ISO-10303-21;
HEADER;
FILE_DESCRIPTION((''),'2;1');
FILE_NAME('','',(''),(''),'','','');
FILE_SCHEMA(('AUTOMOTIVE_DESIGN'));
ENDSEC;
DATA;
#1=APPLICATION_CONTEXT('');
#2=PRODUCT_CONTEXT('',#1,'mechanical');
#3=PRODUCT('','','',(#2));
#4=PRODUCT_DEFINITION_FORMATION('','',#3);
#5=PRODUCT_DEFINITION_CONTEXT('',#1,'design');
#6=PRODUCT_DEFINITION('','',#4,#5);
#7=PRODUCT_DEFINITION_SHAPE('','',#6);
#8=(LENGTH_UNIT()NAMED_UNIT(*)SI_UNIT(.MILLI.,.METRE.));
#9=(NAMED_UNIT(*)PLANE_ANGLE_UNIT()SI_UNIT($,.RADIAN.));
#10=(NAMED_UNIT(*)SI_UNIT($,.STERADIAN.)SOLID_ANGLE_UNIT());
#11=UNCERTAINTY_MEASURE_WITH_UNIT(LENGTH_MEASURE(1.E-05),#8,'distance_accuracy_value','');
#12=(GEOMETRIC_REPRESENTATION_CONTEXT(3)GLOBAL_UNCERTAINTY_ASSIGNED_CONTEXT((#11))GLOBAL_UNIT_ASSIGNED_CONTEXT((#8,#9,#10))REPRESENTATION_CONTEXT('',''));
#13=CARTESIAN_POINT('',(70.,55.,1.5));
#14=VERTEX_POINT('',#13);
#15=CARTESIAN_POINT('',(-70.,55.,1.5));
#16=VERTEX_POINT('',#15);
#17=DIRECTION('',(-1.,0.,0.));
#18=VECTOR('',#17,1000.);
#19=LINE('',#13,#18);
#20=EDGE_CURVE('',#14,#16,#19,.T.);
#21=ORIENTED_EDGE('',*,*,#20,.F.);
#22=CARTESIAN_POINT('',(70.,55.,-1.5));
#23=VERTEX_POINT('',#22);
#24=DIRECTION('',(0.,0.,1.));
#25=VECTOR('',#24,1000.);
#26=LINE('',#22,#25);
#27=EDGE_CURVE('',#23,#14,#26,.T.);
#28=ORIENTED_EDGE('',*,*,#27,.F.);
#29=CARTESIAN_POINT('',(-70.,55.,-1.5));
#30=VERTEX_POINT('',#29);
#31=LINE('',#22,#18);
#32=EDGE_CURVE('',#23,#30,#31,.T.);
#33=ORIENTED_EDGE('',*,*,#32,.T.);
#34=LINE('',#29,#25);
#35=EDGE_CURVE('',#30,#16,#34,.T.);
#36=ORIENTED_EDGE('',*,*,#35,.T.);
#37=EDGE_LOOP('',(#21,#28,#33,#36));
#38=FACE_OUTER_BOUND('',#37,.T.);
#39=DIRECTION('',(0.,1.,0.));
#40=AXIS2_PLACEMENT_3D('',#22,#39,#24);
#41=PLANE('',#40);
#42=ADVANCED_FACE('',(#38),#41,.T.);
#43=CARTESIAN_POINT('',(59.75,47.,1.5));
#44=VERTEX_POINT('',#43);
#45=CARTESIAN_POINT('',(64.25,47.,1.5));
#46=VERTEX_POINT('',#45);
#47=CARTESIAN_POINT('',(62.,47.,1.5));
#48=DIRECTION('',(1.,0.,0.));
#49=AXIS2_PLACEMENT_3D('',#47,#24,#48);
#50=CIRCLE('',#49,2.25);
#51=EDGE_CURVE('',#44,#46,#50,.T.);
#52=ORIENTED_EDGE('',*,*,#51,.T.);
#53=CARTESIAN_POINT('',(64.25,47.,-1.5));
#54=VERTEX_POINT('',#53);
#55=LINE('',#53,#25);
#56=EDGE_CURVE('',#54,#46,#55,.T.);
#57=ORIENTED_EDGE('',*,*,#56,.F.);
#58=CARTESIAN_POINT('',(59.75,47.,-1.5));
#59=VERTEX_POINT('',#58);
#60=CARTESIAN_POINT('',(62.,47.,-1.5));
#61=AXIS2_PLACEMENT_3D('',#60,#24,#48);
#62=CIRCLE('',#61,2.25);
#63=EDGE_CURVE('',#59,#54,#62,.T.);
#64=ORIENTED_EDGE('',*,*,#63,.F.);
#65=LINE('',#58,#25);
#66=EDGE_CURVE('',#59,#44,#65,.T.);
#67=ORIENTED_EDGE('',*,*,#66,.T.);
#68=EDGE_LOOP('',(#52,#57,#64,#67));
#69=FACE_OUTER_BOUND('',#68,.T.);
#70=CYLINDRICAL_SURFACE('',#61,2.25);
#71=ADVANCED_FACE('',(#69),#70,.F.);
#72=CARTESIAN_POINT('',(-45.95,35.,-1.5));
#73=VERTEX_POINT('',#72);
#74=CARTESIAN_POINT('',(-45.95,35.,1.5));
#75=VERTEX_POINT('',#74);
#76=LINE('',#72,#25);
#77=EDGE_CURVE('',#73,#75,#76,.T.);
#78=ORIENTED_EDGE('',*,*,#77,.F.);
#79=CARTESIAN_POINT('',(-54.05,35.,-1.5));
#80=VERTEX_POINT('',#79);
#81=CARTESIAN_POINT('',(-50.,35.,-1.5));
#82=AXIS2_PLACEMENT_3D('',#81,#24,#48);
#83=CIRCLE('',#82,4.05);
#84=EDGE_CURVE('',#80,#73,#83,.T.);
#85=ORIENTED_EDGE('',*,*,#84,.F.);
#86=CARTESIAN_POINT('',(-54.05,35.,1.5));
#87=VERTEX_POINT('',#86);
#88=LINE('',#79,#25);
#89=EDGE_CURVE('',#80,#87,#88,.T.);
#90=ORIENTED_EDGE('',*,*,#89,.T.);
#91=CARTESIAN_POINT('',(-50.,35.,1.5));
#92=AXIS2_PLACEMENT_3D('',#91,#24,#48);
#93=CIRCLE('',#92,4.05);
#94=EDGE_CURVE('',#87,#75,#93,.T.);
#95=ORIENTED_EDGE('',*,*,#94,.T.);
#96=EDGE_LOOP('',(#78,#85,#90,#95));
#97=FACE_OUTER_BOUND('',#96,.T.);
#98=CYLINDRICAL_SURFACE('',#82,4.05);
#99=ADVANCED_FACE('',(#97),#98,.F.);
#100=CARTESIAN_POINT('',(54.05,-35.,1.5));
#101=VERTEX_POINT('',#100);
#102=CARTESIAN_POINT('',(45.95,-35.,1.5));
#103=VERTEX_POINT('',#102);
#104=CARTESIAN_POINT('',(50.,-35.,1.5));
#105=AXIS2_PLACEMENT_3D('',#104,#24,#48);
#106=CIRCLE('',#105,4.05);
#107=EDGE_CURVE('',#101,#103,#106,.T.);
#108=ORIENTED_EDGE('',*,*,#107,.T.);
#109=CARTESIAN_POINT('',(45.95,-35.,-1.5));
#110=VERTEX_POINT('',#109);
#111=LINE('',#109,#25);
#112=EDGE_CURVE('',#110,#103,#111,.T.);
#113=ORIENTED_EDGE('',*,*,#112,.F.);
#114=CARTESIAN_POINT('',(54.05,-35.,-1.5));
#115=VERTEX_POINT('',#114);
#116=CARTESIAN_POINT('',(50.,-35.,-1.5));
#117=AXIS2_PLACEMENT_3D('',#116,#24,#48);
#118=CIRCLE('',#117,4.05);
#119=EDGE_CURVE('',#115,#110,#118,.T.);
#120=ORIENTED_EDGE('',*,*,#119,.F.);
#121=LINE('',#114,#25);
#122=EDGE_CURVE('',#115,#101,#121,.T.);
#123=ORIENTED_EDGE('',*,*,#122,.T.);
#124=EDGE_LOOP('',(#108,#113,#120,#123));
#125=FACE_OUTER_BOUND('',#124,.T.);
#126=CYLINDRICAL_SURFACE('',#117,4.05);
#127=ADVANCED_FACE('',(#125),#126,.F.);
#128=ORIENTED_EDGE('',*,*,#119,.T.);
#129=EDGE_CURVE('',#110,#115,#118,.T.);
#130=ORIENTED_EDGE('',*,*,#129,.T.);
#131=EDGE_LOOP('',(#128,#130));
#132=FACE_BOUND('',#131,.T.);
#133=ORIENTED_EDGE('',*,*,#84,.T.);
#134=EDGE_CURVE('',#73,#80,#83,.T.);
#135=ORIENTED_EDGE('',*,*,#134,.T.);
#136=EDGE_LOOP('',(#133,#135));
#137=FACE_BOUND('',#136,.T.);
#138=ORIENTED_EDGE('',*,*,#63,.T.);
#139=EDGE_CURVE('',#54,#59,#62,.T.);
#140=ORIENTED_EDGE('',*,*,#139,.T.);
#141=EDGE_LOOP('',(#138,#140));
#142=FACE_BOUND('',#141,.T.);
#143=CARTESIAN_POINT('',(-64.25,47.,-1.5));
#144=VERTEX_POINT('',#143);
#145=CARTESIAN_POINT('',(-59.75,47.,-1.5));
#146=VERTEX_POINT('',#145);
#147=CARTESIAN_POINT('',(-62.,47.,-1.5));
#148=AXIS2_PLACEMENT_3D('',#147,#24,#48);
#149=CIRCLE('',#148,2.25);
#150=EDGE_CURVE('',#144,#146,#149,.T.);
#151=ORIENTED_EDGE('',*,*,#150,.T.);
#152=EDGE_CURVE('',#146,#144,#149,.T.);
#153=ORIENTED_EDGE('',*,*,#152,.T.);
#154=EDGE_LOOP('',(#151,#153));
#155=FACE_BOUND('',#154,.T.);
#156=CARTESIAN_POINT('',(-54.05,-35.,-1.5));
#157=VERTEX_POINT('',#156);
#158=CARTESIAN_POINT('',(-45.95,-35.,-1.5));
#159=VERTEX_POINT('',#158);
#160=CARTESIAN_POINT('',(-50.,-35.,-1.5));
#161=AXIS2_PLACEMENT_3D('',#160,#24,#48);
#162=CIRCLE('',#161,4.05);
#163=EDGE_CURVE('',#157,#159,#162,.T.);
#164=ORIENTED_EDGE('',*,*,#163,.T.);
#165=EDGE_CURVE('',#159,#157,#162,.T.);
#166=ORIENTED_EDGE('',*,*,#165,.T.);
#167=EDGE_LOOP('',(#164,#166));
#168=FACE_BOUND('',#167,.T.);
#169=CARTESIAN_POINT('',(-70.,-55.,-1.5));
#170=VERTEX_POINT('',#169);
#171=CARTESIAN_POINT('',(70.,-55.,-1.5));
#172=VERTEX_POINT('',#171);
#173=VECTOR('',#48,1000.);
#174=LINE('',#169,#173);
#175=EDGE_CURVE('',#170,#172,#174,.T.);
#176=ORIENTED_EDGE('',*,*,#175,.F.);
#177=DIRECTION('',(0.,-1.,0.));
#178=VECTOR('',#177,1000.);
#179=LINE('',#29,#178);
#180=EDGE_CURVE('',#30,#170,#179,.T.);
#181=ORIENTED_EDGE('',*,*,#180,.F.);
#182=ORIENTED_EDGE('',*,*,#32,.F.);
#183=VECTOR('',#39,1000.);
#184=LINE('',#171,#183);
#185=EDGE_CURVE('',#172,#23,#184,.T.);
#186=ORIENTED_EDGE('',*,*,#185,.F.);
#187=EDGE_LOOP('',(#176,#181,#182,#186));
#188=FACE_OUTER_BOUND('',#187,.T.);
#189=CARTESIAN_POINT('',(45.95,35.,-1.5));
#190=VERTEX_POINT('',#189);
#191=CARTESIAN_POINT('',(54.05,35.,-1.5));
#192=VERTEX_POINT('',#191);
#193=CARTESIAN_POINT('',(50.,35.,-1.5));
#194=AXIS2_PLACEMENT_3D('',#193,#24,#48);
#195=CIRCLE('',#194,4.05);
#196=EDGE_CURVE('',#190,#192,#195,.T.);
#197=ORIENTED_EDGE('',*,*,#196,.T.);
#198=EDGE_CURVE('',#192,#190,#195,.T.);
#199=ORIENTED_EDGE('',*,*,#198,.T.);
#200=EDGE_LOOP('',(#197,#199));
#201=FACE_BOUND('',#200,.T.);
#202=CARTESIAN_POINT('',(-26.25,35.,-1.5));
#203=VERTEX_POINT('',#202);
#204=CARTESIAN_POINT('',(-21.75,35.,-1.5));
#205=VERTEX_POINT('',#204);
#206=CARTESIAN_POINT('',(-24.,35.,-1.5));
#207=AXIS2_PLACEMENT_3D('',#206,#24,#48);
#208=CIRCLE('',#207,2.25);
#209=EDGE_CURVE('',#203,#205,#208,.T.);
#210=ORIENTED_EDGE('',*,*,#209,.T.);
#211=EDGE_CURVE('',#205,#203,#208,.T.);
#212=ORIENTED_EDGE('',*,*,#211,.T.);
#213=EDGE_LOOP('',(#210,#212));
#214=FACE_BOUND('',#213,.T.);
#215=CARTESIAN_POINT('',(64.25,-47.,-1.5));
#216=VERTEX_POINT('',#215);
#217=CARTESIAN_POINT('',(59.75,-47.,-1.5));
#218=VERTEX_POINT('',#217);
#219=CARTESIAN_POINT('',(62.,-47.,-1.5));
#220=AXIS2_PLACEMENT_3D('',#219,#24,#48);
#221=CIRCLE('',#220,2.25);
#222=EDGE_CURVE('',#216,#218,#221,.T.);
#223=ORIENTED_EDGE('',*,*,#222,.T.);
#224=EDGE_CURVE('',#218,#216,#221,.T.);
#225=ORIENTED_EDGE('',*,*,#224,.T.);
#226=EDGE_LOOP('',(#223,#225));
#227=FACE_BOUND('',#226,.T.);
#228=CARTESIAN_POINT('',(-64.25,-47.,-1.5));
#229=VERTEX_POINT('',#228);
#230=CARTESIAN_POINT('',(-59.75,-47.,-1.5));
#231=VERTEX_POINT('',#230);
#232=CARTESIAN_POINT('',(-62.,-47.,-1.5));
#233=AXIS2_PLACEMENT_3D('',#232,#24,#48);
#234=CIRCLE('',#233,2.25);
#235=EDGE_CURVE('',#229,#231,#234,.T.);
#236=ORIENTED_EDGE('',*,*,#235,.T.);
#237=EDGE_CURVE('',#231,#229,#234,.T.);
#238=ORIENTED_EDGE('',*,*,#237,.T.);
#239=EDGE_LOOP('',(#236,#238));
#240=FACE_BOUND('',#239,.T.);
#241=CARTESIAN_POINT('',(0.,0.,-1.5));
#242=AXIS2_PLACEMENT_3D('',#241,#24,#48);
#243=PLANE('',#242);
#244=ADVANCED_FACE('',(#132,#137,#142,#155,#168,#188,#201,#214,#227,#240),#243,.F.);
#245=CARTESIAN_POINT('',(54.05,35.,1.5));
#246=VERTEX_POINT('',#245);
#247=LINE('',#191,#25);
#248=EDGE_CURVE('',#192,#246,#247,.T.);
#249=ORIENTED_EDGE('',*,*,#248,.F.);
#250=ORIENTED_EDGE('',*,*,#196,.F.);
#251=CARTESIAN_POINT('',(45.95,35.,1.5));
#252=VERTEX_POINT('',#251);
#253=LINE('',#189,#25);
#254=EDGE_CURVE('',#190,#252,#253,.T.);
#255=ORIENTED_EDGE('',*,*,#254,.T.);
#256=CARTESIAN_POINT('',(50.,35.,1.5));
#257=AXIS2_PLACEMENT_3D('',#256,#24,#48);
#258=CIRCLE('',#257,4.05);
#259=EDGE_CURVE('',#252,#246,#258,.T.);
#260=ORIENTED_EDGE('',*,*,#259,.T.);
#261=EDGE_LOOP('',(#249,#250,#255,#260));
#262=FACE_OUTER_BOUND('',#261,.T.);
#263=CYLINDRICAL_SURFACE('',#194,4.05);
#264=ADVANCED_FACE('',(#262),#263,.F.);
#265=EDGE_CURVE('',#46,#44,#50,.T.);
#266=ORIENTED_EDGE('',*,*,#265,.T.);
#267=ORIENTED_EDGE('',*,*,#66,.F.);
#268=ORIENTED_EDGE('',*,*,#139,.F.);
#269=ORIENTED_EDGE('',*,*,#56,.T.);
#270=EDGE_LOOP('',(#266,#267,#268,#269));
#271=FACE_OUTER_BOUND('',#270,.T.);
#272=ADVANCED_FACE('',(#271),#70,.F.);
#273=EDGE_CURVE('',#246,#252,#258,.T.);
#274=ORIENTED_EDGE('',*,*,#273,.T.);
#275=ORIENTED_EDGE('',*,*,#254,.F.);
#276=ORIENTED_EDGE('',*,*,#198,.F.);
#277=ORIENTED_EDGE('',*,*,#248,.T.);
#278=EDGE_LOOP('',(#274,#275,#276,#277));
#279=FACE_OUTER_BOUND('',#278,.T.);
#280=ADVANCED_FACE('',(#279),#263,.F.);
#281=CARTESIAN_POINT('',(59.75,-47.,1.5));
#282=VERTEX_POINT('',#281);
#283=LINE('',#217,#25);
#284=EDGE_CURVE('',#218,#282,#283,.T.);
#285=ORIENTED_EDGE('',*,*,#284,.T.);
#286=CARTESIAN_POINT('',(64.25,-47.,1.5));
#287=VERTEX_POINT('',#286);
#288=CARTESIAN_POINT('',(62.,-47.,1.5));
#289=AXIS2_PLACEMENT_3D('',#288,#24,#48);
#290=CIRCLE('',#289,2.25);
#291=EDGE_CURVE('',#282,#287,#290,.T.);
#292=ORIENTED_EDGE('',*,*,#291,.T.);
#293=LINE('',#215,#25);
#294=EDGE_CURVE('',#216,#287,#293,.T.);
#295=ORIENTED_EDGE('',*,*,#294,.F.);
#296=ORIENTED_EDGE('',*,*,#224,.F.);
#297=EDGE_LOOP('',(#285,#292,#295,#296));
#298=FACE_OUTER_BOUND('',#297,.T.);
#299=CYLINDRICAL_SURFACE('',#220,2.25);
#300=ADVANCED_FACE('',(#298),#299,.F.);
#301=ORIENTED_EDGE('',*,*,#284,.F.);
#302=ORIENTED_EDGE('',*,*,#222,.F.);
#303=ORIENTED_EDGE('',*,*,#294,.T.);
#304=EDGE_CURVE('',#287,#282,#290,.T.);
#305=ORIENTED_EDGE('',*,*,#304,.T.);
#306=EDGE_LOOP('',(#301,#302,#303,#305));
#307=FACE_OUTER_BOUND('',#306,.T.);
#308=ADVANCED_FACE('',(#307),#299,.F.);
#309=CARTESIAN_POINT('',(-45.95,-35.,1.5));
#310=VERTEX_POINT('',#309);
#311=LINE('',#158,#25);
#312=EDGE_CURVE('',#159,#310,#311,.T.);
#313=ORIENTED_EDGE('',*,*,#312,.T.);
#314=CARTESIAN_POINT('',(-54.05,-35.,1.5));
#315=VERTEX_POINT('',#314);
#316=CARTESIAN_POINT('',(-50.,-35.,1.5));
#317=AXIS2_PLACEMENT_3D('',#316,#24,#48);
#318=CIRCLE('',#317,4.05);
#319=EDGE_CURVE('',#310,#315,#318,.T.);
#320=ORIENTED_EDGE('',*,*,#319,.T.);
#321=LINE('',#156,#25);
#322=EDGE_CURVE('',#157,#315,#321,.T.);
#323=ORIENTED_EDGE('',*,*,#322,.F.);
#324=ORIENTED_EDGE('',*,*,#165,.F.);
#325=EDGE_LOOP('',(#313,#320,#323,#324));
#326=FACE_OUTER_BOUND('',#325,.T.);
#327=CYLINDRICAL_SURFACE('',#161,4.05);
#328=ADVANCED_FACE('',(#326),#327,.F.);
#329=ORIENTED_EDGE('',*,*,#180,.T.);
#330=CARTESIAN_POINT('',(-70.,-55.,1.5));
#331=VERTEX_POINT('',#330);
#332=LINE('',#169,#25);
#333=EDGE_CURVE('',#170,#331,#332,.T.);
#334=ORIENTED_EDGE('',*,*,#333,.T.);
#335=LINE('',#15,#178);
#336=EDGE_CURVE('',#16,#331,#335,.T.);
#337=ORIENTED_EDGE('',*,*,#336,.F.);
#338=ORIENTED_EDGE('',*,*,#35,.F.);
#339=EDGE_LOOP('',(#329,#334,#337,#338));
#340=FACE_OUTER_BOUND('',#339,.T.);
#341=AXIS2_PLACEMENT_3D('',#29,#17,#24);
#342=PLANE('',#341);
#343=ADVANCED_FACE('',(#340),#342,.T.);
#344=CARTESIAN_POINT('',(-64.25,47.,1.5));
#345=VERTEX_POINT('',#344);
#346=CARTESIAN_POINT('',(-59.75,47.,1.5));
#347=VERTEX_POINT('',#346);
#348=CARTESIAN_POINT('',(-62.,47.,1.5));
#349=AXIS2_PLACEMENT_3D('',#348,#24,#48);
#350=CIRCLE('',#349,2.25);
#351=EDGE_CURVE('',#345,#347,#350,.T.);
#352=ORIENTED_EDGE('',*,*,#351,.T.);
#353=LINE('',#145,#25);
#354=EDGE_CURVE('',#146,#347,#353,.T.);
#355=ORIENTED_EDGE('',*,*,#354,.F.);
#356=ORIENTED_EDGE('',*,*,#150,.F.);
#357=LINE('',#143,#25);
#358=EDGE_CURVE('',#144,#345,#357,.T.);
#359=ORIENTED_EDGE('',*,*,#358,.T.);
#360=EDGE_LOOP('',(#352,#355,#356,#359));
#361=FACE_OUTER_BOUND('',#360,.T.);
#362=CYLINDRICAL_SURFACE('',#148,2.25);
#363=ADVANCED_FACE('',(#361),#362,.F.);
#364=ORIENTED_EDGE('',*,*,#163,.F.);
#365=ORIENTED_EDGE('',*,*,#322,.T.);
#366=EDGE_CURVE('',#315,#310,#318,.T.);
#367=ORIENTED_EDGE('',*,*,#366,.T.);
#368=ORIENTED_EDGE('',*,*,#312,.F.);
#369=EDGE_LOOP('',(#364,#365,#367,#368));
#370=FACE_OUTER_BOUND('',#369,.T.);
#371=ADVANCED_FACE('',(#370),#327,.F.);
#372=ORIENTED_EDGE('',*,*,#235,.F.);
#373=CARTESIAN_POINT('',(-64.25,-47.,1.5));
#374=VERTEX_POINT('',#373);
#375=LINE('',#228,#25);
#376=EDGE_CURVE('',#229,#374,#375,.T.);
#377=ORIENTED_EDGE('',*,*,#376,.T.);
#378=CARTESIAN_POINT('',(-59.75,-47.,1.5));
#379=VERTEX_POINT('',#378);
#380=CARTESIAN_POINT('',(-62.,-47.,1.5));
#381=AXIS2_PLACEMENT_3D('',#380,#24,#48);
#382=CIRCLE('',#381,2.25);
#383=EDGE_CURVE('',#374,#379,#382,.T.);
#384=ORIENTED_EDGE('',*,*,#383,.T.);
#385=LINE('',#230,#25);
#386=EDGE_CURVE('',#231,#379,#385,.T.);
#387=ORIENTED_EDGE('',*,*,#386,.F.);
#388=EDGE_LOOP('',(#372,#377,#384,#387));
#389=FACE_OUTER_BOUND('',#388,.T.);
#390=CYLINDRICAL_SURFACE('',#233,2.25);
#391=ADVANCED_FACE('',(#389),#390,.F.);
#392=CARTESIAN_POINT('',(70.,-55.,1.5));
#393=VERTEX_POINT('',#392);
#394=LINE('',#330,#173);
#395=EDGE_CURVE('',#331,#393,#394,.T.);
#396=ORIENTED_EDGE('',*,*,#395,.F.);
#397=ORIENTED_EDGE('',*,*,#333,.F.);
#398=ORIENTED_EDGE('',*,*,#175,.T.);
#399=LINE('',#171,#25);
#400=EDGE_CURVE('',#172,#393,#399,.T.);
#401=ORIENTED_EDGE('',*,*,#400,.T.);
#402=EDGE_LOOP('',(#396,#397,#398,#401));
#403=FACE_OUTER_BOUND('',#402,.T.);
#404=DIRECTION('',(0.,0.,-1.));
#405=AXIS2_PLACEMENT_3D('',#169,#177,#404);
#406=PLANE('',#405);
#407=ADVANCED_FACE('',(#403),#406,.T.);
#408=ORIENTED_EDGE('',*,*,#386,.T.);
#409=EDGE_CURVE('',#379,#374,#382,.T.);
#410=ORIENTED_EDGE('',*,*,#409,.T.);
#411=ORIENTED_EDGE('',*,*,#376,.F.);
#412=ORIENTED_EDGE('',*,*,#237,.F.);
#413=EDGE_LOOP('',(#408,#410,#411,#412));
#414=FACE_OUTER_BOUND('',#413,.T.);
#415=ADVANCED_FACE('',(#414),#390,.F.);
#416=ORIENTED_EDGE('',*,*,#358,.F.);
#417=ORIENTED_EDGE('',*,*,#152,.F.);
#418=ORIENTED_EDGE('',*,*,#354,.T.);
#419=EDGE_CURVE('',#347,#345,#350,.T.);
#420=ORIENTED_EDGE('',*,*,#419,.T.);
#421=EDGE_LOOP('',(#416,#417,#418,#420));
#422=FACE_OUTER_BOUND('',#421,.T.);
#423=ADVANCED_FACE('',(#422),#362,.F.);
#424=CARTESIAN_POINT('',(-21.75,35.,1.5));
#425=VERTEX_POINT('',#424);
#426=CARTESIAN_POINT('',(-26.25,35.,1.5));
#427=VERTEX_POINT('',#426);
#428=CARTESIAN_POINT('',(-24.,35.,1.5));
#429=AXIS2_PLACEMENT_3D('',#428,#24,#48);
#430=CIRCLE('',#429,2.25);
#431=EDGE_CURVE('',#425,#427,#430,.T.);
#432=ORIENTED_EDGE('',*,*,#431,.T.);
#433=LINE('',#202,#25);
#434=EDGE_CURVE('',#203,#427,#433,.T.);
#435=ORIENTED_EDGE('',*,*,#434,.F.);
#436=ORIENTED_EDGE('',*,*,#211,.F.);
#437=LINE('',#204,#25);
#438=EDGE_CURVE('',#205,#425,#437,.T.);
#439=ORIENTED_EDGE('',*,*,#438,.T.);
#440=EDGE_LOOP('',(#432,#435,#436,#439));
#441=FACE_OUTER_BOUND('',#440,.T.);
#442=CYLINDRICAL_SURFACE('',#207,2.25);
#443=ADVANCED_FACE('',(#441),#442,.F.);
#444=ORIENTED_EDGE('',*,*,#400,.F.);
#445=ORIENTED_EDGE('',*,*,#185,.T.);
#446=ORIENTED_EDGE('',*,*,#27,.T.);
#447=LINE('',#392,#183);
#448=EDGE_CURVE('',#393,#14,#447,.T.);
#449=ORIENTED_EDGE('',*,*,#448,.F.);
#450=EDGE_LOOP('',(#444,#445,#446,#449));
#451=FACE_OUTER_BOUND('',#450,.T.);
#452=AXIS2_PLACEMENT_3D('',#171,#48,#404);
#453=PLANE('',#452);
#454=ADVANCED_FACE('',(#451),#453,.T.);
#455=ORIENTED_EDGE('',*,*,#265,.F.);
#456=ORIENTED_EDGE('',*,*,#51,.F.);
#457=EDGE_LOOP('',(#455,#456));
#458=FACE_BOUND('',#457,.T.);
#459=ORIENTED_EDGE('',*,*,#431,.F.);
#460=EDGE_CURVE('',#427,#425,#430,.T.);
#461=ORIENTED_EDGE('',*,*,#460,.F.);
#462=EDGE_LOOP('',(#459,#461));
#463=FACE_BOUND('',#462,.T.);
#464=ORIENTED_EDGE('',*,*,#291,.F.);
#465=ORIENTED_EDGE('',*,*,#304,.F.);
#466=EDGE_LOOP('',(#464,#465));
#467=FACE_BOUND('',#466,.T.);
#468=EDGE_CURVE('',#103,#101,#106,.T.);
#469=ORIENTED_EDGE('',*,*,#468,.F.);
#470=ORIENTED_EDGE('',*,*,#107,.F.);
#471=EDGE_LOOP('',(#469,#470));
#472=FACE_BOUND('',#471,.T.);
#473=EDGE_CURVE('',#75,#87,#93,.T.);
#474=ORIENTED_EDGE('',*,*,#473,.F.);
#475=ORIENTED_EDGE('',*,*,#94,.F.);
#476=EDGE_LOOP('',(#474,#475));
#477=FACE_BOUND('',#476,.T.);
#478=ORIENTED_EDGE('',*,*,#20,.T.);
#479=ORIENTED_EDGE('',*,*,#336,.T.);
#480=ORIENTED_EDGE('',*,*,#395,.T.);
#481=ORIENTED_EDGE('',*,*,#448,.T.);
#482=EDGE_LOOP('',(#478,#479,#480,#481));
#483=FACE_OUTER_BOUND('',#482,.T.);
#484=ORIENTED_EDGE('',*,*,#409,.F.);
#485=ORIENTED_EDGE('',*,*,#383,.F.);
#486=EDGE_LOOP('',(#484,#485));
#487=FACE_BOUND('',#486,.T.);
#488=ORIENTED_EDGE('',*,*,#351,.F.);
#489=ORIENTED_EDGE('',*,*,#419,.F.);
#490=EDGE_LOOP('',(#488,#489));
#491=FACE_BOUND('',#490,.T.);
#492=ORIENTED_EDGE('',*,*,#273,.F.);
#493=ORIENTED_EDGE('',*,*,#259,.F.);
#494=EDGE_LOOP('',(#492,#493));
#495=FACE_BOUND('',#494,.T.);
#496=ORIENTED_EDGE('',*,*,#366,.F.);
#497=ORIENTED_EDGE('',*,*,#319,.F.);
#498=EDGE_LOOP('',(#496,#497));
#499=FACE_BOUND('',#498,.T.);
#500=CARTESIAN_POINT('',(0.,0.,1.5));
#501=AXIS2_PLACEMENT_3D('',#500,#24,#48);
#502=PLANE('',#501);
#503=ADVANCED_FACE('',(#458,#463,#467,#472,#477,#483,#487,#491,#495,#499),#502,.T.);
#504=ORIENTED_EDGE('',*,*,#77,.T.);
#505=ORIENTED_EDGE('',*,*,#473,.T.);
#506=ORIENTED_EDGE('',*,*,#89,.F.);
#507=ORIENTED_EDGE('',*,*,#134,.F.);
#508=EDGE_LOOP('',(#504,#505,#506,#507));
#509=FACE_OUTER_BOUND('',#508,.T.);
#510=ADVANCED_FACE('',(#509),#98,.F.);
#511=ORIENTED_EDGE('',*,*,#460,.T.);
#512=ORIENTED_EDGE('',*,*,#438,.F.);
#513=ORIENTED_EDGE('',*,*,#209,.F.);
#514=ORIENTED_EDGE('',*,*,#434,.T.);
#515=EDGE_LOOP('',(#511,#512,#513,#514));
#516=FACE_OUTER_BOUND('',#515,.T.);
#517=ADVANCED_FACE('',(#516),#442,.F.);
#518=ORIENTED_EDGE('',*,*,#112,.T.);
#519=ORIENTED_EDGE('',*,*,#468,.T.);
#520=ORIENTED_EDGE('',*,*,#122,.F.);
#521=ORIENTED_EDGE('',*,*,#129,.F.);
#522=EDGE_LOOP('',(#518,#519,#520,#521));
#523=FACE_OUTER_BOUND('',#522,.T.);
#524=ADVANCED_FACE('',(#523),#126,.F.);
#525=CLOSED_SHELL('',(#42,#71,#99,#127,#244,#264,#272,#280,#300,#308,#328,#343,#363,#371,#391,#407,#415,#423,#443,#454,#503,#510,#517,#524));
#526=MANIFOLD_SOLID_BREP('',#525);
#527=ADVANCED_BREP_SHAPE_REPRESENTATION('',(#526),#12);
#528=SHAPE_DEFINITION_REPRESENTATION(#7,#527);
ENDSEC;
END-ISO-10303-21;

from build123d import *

# Parameters (mm, degrees)
SKETCH_1_W      = 140
SKETCH_1_H      = 110
SKETCH_1_R      = 2.25
SKETCH_1_R_2    = 4.05
EXTRUDE_1_DEPTH = 1.5


with BuildPart() as part:
    # 草图1 → 凸台-拉伸1 (new, symmetric)
    with BuildSketch(Plane.XY):
        Rectangle(SKETCH_1_W, SKETCH_1_H)
        with Locations((-62, -47)):
            Circle(SKETCH_1_R, mode=Mode.SUBTRACT)
        with Locations((-62, 47)):
            Circle(SKETCH_1_R, mode=Mode.SUBTRACT)
        with Locations((62, -47)):
            Circle(SKETCH_1_R, mode=Mode.SUBTRACT)
        with Locations((62, 47)):
            Circle(SKETCH_1_R, mode=Mode.SUBTRACT)
        with Locations((-50, -35)):
            Circle(SKETCH_1_R_2, mode=Mode.SUBTRACT)
        with Locations((-50, 35)):
            Circle(SKETCH_1_R_2, mode=Mode.SUBTRACT)
        with Locations((50, -35)):
            Circle(SKETCH_1_R_2, mode=Mode.SUBTRACT)
        with Locations((50, 35)):
            Circle(SKETCH_1_R_2, mode=Mode.SUBTRACT)
        with Locations((-24, 35)):
            Circle(SKETCH_1_R, mode=Mode.SUBTRACT)
    extrude(amount=EXTRUDE_1_DEPTH, both=True)


solid = part.part
